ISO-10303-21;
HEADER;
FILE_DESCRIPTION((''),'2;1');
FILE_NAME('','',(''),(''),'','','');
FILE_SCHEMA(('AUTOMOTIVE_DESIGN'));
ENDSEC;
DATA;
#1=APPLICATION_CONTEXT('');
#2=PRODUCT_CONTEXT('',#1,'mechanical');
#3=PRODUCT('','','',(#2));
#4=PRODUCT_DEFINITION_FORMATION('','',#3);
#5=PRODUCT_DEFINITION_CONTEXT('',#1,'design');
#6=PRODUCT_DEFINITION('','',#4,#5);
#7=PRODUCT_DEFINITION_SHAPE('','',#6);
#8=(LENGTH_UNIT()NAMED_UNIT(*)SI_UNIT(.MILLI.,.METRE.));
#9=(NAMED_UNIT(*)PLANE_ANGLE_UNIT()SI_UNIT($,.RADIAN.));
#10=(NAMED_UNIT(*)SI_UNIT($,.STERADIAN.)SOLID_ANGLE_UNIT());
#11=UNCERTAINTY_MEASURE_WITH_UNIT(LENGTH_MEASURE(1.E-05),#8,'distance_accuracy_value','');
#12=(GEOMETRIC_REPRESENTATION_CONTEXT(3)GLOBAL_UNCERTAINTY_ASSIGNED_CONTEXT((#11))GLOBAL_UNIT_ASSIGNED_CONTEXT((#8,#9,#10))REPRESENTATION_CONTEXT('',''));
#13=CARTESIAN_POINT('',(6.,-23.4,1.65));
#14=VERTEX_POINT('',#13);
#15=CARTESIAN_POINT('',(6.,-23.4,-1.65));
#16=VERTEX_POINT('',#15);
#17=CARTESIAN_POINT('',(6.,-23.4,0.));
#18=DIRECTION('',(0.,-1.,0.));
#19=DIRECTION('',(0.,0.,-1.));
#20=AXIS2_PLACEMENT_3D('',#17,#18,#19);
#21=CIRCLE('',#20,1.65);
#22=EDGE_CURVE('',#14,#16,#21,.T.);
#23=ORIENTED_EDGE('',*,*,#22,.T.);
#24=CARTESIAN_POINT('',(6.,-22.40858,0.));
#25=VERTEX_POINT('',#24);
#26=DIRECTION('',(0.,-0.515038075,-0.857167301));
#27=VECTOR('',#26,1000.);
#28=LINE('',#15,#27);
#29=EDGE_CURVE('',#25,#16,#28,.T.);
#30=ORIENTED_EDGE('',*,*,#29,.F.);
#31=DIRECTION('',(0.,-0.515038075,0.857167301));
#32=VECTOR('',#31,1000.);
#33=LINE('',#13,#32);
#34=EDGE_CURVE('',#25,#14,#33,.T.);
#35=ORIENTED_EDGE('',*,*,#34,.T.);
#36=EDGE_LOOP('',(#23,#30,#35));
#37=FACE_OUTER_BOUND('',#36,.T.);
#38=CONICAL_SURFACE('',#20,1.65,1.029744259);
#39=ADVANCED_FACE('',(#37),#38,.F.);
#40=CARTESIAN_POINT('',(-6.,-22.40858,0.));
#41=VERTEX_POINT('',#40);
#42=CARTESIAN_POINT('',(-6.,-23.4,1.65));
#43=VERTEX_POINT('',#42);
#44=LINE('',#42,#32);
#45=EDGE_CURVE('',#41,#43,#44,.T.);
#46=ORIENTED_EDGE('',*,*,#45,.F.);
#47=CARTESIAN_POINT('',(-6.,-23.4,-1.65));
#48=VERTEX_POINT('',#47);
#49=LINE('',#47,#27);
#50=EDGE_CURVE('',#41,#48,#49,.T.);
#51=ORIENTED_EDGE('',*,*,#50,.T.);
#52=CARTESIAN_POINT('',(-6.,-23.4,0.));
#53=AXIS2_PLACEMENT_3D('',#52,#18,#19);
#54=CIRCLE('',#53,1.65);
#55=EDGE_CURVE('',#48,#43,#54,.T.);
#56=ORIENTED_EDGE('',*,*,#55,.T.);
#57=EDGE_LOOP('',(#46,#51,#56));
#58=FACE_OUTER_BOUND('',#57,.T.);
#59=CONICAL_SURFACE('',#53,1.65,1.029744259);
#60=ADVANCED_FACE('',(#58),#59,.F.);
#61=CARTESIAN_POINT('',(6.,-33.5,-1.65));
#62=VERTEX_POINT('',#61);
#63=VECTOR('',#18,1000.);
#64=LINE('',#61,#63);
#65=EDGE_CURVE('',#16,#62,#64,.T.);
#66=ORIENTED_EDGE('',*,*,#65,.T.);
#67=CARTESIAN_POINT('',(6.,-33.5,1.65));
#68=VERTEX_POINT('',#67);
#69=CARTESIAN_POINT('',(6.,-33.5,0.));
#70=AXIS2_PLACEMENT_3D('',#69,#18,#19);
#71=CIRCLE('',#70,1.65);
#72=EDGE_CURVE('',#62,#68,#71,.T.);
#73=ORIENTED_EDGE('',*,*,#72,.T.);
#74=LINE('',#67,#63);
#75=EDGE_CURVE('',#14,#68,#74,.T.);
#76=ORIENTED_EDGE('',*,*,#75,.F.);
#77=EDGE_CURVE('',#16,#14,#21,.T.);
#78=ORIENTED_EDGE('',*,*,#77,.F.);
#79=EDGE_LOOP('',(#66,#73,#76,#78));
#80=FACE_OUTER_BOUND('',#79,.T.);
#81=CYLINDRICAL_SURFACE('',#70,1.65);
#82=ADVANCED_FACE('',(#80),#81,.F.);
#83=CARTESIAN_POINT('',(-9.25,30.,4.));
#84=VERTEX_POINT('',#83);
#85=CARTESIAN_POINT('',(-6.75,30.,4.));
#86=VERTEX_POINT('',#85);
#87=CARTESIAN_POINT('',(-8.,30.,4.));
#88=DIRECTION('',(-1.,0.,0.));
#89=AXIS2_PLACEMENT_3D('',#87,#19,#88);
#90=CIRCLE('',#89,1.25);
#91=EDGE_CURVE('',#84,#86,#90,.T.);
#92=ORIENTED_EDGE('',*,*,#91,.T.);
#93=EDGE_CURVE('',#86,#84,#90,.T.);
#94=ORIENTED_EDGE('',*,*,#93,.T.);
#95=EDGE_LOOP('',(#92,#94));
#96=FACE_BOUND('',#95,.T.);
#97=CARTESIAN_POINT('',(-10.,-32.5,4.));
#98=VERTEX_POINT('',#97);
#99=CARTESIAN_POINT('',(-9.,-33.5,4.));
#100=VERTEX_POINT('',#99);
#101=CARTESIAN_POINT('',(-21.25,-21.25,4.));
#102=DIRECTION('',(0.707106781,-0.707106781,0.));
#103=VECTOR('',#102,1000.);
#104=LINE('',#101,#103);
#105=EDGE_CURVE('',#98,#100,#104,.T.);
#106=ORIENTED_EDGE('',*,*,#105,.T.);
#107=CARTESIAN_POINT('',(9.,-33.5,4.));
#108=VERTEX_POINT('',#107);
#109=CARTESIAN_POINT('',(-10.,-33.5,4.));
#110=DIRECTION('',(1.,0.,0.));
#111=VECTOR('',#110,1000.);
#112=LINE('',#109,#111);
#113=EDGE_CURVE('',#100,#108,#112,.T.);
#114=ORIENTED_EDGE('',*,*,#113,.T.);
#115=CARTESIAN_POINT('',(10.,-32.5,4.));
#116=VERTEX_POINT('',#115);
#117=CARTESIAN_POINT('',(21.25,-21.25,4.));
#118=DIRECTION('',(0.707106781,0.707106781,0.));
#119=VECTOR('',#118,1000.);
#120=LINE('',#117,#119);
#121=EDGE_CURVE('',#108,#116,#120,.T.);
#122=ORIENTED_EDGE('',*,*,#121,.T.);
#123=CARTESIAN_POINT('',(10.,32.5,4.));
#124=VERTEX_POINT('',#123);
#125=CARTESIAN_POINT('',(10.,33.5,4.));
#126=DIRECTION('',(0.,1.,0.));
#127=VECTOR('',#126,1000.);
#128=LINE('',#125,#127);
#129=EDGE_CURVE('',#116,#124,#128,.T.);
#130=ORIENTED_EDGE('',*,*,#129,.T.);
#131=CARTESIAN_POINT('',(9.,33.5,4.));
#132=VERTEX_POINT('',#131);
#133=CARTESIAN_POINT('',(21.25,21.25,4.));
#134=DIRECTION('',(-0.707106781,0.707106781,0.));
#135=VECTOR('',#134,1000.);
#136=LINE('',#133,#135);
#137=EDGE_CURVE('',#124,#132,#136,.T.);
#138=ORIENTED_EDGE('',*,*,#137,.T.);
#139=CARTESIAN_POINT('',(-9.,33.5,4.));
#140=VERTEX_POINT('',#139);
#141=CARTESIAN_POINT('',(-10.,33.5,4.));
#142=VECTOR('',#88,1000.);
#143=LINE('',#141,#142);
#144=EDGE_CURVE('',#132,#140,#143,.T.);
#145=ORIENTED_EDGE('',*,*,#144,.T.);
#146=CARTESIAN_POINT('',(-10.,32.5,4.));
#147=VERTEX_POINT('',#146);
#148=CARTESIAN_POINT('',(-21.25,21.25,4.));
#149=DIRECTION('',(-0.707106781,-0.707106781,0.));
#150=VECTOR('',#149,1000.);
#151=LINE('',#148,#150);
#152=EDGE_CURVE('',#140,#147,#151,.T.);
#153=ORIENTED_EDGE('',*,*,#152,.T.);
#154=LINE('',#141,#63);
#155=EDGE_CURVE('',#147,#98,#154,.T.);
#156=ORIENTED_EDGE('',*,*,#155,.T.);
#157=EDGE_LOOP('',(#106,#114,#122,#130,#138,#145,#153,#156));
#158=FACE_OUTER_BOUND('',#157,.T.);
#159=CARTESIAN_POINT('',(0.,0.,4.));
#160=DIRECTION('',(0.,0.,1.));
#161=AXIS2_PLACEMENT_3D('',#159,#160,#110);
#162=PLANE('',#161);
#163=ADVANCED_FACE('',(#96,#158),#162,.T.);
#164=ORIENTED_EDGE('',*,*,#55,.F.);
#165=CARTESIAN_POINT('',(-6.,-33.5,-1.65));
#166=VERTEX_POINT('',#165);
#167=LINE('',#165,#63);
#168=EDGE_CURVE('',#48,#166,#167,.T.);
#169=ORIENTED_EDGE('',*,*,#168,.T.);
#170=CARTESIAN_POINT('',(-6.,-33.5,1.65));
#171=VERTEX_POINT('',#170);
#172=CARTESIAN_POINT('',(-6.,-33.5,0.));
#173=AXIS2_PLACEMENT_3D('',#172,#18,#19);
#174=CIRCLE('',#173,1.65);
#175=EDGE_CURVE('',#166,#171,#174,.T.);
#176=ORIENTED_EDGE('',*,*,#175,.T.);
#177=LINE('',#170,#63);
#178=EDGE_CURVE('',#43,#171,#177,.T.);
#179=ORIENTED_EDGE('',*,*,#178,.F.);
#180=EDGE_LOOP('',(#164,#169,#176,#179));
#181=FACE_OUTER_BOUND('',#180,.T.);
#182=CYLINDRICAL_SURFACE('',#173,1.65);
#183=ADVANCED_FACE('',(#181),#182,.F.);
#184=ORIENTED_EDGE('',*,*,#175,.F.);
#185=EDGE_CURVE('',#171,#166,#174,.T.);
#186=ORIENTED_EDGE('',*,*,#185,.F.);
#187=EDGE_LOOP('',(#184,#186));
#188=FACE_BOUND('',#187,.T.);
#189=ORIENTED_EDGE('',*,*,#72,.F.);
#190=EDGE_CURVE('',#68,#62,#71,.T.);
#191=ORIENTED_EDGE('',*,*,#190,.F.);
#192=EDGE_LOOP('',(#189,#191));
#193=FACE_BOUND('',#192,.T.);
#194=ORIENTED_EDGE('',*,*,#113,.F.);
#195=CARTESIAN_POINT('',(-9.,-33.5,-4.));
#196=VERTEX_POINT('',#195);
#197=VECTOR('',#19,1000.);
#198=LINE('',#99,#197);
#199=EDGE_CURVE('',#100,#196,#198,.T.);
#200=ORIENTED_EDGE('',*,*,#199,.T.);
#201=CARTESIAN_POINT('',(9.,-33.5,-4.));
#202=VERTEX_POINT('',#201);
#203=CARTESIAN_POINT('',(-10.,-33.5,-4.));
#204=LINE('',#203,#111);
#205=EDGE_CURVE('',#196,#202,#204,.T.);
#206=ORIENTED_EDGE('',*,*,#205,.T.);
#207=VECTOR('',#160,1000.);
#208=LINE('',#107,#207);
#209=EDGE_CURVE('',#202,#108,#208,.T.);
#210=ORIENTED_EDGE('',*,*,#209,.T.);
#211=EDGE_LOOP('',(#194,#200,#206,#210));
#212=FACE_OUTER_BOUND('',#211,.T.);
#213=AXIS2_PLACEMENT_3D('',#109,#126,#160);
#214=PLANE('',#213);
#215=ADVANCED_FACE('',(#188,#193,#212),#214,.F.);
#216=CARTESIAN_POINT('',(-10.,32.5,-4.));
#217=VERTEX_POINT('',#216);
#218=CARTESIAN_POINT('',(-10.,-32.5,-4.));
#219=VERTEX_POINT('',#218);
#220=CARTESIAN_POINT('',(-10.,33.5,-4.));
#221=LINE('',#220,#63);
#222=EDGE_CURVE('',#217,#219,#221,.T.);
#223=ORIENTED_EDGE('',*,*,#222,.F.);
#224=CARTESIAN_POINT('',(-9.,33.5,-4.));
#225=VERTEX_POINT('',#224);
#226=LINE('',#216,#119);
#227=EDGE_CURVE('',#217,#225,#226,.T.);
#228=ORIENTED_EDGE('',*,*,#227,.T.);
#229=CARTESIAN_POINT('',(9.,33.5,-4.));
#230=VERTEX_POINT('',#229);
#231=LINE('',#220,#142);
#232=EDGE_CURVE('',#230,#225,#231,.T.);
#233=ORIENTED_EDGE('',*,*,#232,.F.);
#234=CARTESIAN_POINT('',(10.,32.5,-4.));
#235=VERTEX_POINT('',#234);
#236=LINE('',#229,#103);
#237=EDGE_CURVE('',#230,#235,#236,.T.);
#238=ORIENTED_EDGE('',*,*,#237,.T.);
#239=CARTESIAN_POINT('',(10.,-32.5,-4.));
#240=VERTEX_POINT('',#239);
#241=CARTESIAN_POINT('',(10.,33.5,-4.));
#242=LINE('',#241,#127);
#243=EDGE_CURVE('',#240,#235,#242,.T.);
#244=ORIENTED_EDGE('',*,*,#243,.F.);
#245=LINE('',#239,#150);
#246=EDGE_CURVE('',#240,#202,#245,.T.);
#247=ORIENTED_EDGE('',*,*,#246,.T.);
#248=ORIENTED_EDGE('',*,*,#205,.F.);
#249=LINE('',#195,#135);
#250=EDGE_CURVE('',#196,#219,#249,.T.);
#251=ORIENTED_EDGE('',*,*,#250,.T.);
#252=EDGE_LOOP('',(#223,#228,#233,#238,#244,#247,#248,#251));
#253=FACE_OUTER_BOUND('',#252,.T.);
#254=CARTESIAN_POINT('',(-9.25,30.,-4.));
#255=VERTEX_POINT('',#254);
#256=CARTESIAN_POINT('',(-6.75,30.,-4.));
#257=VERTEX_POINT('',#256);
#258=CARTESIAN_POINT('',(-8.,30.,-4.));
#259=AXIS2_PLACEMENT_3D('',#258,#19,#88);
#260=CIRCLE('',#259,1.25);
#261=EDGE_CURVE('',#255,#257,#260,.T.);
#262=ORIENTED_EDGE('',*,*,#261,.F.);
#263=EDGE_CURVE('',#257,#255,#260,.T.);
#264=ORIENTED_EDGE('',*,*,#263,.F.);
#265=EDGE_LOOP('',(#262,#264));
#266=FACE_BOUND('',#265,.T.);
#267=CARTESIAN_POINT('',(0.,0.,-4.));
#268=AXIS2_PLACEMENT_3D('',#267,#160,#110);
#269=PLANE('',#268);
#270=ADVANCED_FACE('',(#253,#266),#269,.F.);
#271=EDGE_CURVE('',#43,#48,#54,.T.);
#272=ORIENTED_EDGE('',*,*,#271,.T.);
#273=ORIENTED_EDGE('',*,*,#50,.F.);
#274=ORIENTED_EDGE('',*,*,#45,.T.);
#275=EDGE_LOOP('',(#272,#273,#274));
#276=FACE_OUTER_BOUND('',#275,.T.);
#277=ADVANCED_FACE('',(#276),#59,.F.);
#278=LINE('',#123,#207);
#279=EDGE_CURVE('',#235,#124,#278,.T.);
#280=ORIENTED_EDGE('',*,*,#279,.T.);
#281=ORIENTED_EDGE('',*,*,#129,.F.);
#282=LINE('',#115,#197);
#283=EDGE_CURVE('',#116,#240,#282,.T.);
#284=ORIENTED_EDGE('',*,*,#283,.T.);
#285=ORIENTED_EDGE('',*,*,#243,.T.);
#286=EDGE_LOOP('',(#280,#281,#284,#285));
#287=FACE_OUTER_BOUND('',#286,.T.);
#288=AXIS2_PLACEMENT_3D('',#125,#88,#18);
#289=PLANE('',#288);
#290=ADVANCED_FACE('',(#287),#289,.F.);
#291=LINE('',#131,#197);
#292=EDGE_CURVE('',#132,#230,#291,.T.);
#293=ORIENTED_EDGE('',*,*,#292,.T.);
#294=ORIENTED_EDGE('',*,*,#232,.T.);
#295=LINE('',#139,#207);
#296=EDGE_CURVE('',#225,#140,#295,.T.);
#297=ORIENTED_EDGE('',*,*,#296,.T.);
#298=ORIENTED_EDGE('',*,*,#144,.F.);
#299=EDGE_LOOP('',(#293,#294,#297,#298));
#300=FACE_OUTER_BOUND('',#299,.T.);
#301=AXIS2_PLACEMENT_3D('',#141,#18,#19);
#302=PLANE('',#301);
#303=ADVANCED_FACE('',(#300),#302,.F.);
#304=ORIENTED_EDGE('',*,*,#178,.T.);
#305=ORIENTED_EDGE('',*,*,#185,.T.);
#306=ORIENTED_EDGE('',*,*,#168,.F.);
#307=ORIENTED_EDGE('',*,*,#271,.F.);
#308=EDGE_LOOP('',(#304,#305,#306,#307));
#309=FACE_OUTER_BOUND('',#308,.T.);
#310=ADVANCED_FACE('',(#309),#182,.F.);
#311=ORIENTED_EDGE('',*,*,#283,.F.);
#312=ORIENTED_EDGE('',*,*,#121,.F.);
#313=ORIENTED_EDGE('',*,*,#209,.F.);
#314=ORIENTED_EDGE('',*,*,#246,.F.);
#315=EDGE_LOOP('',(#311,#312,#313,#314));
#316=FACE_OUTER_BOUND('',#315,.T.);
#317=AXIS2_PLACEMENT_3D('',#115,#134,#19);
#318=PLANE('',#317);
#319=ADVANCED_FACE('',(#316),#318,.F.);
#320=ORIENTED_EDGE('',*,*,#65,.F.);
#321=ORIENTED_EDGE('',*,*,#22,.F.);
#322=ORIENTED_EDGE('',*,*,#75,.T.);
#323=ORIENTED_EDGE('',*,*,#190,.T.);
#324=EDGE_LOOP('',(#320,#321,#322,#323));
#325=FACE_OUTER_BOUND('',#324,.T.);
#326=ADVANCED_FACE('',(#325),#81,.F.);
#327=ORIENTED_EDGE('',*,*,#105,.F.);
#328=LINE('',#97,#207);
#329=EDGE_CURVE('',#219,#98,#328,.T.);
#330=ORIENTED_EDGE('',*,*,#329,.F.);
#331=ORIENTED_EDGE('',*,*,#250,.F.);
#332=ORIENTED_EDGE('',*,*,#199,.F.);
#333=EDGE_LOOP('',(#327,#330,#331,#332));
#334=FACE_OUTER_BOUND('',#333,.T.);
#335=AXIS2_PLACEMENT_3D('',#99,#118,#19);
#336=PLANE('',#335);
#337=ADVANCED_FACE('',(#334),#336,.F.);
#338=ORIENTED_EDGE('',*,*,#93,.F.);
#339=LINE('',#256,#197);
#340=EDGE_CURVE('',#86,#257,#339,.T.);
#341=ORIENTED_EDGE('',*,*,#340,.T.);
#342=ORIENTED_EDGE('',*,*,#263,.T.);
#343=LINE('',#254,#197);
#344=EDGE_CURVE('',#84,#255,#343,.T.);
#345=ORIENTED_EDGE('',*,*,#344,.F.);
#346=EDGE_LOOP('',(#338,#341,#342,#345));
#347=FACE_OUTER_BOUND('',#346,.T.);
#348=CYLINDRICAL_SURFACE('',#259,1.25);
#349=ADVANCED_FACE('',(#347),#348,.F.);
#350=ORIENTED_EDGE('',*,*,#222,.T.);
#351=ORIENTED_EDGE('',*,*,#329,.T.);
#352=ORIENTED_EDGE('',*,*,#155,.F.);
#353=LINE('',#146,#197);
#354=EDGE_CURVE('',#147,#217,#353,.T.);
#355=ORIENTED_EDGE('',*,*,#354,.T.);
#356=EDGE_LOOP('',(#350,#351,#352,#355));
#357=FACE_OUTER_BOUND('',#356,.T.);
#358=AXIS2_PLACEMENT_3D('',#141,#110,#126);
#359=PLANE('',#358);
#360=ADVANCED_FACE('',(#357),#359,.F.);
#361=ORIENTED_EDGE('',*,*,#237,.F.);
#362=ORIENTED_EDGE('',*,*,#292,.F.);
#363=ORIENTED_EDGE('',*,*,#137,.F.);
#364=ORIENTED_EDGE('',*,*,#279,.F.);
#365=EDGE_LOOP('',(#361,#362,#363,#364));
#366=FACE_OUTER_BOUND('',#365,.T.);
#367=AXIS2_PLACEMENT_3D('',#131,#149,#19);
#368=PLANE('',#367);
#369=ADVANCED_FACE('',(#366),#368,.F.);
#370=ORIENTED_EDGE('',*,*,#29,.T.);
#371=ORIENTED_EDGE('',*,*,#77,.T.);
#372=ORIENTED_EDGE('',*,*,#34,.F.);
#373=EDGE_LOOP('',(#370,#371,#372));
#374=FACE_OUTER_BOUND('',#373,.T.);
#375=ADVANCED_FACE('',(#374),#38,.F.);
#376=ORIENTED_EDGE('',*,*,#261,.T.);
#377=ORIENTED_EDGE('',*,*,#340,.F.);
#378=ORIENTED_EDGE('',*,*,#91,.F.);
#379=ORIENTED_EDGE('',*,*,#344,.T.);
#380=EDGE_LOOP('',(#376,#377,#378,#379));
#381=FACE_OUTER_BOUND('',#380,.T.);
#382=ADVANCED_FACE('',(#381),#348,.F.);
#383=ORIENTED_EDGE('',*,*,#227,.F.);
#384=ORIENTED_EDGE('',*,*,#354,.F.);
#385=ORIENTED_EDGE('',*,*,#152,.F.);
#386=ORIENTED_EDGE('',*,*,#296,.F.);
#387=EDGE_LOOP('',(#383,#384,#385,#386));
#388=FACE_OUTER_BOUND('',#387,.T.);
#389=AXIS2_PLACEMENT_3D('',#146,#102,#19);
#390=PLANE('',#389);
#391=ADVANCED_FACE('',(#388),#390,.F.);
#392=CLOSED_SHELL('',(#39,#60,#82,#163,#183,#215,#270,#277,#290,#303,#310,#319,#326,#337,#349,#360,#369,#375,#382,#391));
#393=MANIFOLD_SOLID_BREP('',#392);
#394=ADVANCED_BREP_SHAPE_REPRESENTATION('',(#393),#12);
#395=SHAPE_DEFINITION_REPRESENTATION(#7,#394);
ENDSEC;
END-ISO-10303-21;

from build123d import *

# Parameters (mm, degrees)
SKETCH_1_W             = 20
SKETCH_1_H             = 67
EXTRUDE_1_DEPTH        = 4
HOLE_WIZARD_M3_1_D     = 2.5
HOLE_WIZARD_M4_1_D     = 3.3
HOLE_WIZARD_M4_1_DEPTH = 10.1
HOLE_WIZARD_M4_1_TIP   = 0.991420021
CHAMFER_1_SIZE         = 1


with BuildPart() as part:
    # 草图1 → 凸台-拉伸1 (new, symmetric)
    with BuildSketch(Plane.XY):
        Rectangle(SKETCH_1_W, SKETCH_1_H)
    extrude(amount=EXTRUDE_1_DEPTH, both=True)

    # M3 螺纹孔1 (through all)
    with Locations(Plane(origin=(0, 0, -4), x_dir=(-1, 0, 0), z_dir=(0, 0, -1))):
        with Locations((8, 30)):
            Hole(HOLE_WIZARD_M3_1_D / 2)

    # M4 螺纹孔1
    with Locations(Plane(origin=(0, -33.5, 0), x_dir=(-1, 0, 0), z_dir=(0, -1, 0))):
        with Locations((6, 0), (-6, 0)):
            Hole(HOLE_WIZARD_M4_1_D / 2, depth=HOLE_WIZARD_M4_1_DEPTH)
            with Locations((0, 0, -(HOLE_WIZARD_M4_1_DEPTH + HOLE_WIZARD_M4_1_TIP / 2))):  # 118° drill point
                Cone(0, HOLE_WIZARD_M4_1_D / 2, HOLE_WIZARD_M4_1_TIP, mode=Mode.SUBTRACT)

    # 倒角1
    chamfer_1_edges = [part.edges().sort_by_distance(p)[0] for p in [
        (10, -33.5, 0),
        (-10, -33.5, 0),
        (-10, 33.5, 0),
        (10, 33.5, 0),
    ]]
    chamfer(chamfer_1_edges, length=CHAMFER_1_SIZE)


solid = part.part
